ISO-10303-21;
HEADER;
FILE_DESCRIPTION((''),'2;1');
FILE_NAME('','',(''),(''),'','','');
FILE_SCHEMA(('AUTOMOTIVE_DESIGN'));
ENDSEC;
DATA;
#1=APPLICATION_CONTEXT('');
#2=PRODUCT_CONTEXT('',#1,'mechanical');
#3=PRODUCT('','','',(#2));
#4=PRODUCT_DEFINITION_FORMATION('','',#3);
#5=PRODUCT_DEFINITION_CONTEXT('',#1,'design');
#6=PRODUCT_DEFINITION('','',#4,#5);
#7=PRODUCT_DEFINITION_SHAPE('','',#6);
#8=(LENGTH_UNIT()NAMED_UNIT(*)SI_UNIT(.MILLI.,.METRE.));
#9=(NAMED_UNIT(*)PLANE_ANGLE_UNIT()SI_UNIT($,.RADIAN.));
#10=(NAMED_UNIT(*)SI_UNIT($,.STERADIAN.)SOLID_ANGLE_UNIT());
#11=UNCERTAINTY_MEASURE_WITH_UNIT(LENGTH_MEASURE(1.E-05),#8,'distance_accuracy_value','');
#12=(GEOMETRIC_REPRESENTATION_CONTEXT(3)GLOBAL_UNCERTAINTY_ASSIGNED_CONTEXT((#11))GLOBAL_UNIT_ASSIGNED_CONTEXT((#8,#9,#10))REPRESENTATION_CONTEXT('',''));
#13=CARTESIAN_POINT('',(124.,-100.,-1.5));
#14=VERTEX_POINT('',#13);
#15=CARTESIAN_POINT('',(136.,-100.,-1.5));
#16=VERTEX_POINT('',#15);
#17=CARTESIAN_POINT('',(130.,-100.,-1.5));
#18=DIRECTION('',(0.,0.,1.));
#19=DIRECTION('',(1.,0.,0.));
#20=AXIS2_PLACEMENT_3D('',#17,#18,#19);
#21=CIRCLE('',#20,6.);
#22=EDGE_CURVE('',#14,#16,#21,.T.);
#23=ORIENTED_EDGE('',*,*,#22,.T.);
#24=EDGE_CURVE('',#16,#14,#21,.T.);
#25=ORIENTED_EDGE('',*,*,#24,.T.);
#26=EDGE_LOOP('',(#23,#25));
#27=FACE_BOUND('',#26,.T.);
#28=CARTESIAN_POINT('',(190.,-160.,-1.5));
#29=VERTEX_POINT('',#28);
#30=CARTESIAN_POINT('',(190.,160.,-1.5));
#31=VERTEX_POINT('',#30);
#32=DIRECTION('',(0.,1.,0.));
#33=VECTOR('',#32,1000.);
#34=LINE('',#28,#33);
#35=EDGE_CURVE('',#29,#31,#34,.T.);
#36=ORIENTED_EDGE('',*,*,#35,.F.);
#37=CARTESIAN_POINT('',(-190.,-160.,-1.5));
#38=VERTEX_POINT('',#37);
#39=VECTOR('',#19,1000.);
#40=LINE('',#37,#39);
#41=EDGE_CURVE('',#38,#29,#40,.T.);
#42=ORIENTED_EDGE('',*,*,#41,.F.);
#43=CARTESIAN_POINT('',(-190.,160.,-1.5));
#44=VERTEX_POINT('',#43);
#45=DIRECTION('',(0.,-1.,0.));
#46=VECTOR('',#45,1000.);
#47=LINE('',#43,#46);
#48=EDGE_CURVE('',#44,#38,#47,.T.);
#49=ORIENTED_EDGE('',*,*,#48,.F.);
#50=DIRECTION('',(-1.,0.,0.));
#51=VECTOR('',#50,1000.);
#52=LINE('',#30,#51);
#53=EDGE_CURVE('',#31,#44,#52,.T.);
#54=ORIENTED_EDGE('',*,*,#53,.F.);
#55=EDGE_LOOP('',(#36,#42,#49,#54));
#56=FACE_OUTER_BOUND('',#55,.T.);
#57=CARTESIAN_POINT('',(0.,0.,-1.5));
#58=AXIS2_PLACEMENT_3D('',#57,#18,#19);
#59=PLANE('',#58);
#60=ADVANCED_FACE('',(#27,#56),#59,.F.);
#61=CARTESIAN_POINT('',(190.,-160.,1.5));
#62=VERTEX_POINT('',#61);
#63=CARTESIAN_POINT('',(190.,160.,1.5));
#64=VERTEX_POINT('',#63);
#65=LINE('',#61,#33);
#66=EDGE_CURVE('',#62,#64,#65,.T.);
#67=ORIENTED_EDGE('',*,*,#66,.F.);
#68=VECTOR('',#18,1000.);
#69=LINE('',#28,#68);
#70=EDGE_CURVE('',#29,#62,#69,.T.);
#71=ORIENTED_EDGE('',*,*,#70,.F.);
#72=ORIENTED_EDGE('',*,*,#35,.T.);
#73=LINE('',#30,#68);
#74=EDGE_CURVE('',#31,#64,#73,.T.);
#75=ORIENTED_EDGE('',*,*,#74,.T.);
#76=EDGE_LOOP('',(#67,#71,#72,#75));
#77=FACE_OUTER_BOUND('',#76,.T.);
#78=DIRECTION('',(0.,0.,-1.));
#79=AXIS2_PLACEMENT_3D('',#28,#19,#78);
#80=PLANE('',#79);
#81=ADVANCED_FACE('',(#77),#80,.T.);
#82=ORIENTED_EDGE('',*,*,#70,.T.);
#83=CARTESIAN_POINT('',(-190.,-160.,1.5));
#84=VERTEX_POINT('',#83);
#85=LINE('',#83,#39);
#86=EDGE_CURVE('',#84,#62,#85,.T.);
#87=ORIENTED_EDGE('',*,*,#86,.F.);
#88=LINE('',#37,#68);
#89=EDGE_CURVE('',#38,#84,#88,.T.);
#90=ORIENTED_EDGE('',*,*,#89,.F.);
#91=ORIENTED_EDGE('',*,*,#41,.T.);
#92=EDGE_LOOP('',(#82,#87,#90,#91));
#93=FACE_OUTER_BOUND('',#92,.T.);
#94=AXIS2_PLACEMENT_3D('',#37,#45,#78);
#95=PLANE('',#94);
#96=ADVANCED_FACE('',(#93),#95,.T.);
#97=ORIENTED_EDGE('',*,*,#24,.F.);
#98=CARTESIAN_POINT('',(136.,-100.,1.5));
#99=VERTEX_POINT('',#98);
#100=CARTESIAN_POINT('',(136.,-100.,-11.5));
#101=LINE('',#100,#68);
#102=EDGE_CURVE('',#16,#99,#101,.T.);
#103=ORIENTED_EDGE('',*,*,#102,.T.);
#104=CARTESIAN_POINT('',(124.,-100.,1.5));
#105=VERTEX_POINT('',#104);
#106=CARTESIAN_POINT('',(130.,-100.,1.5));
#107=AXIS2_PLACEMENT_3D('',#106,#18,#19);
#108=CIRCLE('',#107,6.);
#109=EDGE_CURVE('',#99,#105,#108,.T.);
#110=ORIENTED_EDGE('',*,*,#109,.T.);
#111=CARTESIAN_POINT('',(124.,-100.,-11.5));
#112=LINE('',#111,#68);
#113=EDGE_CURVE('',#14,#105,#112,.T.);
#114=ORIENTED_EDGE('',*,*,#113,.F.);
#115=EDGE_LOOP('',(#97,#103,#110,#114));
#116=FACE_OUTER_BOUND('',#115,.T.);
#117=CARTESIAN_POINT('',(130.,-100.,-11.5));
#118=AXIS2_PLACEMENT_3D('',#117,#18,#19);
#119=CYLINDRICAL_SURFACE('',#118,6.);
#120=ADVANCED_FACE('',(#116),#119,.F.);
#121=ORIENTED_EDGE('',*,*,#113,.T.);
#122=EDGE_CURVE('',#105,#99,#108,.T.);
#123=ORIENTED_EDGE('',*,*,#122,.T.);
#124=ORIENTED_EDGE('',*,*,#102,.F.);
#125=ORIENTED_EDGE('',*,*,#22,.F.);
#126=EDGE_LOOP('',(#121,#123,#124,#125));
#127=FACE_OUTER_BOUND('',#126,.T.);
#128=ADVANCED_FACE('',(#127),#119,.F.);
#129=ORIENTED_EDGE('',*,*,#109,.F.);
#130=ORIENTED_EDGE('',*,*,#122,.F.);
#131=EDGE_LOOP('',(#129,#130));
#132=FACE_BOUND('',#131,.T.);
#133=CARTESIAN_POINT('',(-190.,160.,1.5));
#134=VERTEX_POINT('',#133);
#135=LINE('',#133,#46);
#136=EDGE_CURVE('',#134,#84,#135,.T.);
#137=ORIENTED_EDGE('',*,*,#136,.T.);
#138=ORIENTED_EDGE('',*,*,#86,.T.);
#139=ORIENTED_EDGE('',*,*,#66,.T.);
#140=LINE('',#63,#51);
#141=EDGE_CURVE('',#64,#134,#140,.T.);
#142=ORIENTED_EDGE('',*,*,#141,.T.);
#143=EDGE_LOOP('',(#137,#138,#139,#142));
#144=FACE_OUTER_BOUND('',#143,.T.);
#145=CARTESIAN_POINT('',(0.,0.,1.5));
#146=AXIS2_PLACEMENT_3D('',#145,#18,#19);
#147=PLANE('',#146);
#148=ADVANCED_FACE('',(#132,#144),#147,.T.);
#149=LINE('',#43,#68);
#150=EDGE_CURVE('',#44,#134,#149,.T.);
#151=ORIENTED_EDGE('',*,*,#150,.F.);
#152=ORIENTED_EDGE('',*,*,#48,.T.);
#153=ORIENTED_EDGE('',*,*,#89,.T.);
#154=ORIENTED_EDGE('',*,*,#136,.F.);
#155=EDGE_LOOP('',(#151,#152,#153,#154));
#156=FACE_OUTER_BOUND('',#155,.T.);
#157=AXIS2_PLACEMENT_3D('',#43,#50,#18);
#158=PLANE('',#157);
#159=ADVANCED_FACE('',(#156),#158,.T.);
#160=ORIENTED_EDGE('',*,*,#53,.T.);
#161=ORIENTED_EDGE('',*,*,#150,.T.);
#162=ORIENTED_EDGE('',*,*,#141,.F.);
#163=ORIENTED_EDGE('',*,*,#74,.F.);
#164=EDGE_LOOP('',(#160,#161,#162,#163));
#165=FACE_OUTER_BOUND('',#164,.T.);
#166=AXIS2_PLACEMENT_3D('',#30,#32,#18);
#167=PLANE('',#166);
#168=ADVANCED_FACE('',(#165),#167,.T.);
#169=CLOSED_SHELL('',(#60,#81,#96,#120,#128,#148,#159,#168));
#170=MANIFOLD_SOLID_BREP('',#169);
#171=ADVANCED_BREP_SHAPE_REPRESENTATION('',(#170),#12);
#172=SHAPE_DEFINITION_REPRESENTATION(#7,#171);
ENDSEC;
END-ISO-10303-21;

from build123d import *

# Parameters (mm, degrees)
SKETCH_1_W          = 380
SKETCH_1_H          = 320
EXTRUDE_1_DEPTH     = 1.5
SKETCH_2_R          = 6
CUT_EXTRUDE_1_DEPTH = 11.5


with BuildPart() as part:
    # 草图1 → 凸台-拉伸1 (new, symmetric)
    with BuildSketch(Plane.XY):
        Rectangle(SKETCH_1_W, SKETCH_1_H)
    extrude(amount=EXTRUDE_1_DEPTH, both=True)

    # 草图2 → 切除-拉伸1 (cut, symmetric)
    with BuildSketch(Plane.XY):
        with Locations((130, -100)):
            Circle(SKETCH_2_R)
    extrude(amount=CUT_EXTRUDE_1_DEPTH, both=True, mode=Mode.SUBTRACT)


solid = part.part
